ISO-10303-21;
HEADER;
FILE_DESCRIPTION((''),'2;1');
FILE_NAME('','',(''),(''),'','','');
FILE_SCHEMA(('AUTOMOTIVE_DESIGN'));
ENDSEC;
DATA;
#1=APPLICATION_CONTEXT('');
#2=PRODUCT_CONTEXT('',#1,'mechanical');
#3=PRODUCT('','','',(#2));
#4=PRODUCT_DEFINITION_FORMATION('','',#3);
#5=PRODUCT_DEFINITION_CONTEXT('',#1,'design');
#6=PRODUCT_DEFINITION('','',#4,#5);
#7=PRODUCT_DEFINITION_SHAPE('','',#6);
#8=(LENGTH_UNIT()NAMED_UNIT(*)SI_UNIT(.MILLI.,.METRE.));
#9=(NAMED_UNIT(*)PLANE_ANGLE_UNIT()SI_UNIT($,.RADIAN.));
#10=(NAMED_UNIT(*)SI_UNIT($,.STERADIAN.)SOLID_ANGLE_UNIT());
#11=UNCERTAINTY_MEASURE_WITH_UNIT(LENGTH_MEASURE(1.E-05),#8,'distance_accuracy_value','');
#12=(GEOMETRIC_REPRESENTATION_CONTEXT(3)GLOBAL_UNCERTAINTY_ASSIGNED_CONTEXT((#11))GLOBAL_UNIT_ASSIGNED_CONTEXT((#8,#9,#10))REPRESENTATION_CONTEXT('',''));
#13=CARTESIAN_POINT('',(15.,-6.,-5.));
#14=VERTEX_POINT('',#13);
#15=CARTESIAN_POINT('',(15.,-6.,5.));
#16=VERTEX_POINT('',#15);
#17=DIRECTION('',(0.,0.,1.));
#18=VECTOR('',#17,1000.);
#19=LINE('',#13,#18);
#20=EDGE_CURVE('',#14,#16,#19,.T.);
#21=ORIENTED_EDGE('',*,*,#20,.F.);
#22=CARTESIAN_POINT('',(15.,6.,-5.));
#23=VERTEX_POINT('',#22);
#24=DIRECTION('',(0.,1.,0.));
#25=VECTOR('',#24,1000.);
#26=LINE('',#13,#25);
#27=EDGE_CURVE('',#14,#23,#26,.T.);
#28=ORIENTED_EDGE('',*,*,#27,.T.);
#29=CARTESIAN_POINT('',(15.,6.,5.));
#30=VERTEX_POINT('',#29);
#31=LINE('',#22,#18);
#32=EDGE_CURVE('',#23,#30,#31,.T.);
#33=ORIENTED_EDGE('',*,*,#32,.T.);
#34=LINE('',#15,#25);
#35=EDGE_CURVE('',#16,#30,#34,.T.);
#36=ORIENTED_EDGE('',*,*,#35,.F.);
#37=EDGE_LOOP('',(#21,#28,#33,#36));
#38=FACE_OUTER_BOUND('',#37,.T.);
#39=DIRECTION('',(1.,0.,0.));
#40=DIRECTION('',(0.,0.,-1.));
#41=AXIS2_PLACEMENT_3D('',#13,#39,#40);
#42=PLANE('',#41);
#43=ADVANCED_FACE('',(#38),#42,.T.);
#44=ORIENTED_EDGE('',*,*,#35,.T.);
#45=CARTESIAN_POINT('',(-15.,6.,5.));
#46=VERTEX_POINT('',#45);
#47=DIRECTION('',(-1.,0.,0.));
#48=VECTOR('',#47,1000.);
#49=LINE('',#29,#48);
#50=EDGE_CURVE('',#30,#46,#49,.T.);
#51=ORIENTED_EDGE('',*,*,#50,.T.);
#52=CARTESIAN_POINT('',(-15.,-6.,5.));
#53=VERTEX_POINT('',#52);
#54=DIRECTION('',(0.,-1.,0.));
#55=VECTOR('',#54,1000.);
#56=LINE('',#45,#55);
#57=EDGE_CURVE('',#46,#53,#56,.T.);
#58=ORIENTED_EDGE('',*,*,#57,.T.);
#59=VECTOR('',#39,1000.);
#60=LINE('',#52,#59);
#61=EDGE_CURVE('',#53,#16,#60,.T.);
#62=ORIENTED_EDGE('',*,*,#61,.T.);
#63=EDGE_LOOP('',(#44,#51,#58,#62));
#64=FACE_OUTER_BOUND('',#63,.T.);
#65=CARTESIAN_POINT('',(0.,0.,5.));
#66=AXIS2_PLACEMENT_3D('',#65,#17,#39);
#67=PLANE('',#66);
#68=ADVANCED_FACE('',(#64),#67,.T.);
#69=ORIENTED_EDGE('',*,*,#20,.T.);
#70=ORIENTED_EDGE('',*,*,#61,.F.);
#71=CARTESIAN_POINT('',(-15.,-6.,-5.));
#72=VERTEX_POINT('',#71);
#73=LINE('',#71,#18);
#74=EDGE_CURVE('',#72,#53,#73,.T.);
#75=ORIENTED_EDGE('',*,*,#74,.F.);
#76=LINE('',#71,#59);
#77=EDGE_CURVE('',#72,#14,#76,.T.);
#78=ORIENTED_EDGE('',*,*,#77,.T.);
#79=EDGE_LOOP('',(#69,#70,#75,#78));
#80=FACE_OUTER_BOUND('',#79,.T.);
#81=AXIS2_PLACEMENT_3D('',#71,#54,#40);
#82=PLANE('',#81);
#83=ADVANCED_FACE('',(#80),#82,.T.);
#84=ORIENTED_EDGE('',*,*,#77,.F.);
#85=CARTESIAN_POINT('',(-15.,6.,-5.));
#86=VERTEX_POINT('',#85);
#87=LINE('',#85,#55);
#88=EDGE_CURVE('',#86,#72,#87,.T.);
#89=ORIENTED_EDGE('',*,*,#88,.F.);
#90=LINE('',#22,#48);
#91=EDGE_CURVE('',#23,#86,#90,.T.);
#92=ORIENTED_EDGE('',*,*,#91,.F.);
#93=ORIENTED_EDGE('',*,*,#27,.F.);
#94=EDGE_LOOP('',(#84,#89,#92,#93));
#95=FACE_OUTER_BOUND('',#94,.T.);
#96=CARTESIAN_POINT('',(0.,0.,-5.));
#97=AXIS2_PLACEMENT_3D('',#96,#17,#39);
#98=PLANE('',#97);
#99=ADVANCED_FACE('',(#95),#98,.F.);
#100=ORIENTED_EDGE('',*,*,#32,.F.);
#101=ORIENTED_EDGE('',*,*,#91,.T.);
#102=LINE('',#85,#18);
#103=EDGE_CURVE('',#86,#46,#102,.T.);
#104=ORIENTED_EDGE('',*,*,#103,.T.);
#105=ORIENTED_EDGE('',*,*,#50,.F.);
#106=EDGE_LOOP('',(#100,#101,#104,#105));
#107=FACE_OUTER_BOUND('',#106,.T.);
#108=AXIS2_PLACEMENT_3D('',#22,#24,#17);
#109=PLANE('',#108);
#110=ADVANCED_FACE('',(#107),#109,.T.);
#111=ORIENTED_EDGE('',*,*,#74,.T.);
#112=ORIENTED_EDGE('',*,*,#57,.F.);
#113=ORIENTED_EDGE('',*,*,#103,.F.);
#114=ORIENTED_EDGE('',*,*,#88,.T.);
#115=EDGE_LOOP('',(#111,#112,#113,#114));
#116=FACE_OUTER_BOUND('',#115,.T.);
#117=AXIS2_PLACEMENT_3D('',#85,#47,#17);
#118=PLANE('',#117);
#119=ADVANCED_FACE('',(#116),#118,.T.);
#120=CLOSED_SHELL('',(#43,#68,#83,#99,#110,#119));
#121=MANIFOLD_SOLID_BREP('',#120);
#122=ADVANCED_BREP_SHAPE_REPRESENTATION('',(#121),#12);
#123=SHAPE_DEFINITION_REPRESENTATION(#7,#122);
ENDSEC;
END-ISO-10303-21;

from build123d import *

# Parameters (mm, degrees)
SKETCH_1_W      = 30
SKETCH_1_H      = 12
EXTRUDE_1_DEPTH = 5


with BuildPart() as part:
    # 草图1 → 凸台-拉伸1 (new, symmetric)
    with BuildSketch(Plane.XY):
        Rectangle(SKETCH_1_W, SKETCH_1_H)
    extrude(amount=EXTRUDE_1_DEPTH, both=True)


solid = part.part
